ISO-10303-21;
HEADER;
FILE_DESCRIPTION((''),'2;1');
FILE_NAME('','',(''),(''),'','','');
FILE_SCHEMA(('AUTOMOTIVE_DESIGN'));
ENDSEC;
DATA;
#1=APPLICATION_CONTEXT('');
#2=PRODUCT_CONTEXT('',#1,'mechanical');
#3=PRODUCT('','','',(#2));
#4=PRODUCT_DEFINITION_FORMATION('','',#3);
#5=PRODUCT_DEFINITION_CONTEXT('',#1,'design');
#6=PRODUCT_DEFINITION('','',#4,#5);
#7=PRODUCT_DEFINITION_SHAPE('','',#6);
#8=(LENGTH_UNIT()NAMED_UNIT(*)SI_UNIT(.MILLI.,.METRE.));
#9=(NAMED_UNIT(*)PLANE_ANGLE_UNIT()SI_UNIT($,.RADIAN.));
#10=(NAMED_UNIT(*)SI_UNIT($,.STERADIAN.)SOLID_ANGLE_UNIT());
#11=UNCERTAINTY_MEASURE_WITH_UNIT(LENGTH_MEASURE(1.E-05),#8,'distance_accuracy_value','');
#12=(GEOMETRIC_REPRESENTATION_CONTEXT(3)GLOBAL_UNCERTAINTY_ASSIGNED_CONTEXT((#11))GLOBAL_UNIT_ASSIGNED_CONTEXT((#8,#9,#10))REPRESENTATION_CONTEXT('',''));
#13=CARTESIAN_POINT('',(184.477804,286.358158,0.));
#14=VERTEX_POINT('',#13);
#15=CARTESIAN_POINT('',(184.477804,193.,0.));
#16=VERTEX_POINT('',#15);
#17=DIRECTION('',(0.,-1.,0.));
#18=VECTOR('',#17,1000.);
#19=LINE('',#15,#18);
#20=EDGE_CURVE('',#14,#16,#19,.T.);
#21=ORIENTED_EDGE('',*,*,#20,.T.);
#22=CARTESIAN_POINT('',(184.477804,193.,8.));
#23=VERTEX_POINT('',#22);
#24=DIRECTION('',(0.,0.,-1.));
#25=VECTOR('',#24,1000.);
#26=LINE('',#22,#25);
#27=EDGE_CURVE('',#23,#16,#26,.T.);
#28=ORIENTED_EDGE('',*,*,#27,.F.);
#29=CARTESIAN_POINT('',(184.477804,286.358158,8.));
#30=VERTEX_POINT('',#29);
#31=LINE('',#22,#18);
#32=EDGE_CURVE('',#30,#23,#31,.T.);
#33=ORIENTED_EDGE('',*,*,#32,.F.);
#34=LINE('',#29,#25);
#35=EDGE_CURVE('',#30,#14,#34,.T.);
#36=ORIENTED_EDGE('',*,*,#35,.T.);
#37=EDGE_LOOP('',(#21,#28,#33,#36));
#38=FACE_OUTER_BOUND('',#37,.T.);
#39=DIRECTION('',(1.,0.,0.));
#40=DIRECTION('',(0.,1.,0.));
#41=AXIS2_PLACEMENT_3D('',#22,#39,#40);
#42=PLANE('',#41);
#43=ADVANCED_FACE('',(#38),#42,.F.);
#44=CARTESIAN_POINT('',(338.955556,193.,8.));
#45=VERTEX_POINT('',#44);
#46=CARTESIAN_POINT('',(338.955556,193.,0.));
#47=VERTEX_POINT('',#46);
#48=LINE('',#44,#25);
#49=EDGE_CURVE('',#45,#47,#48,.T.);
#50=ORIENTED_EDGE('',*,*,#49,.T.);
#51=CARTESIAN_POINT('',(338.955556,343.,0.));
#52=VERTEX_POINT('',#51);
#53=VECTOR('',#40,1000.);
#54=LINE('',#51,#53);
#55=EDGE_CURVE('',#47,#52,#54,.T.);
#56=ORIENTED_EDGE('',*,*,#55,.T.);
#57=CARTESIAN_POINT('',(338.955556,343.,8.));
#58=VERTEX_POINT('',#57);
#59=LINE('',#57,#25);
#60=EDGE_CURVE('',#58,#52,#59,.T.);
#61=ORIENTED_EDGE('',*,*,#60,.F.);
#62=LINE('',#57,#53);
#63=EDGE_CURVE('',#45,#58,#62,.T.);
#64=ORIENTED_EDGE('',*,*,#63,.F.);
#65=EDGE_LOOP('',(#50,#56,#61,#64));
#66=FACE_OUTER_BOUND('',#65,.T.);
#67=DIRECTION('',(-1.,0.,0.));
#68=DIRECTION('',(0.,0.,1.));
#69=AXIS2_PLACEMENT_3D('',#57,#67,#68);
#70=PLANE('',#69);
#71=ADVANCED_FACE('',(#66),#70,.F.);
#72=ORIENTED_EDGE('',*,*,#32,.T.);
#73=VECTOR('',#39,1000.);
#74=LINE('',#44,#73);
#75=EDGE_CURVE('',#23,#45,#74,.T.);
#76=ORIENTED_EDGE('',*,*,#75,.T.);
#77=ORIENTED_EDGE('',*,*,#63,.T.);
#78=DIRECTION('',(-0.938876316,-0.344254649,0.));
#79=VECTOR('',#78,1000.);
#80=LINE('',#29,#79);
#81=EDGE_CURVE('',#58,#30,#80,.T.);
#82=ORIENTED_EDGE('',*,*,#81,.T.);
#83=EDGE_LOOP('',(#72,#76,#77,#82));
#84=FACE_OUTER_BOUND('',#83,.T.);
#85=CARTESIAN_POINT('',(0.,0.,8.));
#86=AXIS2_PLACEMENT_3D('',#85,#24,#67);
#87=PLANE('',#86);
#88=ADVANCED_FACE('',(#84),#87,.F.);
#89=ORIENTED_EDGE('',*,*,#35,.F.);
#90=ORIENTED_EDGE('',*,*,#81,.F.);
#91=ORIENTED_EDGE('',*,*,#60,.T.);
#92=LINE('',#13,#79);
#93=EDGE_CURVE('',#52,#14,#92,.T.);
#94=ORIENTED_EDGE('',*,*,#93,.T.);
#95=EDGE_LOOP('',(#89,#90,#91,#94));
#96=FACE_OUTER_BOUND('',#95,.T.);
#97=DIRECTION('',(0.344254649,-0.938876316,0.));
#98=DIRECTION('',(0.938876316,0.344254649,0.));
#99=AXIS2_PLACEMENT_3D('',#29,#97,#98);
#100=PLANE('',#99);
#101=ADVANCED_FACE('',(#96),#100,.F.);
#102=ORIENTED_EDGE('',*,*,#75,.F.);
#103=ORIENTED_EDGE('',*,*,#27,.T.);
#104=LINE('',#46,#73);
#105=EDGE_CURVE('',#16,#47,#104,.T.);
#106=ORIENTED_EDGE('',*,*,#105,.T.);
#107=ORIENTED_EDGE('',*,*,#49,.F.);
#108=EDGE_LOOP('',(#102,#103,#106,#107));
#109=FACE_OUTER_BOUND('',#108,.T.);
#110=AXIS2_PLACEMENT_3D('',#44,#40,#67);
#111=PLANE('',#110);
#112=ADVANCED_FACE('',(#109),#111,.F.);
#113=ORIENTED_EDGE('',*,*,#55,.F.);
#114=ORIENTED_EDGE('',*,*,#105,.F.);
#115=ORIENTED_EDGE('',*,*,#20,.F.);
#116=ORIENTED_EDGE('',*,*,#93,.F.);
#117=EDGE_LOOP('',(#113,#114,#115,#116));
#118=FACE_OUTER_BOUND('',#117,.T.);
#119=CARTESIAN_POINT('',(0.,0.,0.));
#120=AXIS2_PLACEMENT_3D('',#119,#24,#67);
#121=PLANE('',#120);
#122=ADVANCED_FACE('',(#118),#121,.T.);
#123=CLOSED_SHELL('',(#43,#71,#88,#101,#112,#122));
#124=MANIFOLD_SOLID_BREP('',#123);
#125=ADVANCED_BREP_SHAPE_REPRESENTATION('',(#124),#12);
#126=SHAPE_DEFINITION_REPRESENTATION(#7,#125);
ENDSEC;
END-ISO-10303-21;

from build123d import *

# Parameters (mm, degrees)
EXTRUDE_1_DEPTH = 8


with BuildPart() as part:
    # 草图1 → 凸台-拉伸1 (new body)
    with BuildSketch(Plane.XY):
        Polygon((184.477803528, 193), (184.477803528, 286.35815759), (338.955555556, 343), (338.955555556, 193), align=None)
    extrude(amount=EXTRUDE_1_DEPTH)


solid = part.part
